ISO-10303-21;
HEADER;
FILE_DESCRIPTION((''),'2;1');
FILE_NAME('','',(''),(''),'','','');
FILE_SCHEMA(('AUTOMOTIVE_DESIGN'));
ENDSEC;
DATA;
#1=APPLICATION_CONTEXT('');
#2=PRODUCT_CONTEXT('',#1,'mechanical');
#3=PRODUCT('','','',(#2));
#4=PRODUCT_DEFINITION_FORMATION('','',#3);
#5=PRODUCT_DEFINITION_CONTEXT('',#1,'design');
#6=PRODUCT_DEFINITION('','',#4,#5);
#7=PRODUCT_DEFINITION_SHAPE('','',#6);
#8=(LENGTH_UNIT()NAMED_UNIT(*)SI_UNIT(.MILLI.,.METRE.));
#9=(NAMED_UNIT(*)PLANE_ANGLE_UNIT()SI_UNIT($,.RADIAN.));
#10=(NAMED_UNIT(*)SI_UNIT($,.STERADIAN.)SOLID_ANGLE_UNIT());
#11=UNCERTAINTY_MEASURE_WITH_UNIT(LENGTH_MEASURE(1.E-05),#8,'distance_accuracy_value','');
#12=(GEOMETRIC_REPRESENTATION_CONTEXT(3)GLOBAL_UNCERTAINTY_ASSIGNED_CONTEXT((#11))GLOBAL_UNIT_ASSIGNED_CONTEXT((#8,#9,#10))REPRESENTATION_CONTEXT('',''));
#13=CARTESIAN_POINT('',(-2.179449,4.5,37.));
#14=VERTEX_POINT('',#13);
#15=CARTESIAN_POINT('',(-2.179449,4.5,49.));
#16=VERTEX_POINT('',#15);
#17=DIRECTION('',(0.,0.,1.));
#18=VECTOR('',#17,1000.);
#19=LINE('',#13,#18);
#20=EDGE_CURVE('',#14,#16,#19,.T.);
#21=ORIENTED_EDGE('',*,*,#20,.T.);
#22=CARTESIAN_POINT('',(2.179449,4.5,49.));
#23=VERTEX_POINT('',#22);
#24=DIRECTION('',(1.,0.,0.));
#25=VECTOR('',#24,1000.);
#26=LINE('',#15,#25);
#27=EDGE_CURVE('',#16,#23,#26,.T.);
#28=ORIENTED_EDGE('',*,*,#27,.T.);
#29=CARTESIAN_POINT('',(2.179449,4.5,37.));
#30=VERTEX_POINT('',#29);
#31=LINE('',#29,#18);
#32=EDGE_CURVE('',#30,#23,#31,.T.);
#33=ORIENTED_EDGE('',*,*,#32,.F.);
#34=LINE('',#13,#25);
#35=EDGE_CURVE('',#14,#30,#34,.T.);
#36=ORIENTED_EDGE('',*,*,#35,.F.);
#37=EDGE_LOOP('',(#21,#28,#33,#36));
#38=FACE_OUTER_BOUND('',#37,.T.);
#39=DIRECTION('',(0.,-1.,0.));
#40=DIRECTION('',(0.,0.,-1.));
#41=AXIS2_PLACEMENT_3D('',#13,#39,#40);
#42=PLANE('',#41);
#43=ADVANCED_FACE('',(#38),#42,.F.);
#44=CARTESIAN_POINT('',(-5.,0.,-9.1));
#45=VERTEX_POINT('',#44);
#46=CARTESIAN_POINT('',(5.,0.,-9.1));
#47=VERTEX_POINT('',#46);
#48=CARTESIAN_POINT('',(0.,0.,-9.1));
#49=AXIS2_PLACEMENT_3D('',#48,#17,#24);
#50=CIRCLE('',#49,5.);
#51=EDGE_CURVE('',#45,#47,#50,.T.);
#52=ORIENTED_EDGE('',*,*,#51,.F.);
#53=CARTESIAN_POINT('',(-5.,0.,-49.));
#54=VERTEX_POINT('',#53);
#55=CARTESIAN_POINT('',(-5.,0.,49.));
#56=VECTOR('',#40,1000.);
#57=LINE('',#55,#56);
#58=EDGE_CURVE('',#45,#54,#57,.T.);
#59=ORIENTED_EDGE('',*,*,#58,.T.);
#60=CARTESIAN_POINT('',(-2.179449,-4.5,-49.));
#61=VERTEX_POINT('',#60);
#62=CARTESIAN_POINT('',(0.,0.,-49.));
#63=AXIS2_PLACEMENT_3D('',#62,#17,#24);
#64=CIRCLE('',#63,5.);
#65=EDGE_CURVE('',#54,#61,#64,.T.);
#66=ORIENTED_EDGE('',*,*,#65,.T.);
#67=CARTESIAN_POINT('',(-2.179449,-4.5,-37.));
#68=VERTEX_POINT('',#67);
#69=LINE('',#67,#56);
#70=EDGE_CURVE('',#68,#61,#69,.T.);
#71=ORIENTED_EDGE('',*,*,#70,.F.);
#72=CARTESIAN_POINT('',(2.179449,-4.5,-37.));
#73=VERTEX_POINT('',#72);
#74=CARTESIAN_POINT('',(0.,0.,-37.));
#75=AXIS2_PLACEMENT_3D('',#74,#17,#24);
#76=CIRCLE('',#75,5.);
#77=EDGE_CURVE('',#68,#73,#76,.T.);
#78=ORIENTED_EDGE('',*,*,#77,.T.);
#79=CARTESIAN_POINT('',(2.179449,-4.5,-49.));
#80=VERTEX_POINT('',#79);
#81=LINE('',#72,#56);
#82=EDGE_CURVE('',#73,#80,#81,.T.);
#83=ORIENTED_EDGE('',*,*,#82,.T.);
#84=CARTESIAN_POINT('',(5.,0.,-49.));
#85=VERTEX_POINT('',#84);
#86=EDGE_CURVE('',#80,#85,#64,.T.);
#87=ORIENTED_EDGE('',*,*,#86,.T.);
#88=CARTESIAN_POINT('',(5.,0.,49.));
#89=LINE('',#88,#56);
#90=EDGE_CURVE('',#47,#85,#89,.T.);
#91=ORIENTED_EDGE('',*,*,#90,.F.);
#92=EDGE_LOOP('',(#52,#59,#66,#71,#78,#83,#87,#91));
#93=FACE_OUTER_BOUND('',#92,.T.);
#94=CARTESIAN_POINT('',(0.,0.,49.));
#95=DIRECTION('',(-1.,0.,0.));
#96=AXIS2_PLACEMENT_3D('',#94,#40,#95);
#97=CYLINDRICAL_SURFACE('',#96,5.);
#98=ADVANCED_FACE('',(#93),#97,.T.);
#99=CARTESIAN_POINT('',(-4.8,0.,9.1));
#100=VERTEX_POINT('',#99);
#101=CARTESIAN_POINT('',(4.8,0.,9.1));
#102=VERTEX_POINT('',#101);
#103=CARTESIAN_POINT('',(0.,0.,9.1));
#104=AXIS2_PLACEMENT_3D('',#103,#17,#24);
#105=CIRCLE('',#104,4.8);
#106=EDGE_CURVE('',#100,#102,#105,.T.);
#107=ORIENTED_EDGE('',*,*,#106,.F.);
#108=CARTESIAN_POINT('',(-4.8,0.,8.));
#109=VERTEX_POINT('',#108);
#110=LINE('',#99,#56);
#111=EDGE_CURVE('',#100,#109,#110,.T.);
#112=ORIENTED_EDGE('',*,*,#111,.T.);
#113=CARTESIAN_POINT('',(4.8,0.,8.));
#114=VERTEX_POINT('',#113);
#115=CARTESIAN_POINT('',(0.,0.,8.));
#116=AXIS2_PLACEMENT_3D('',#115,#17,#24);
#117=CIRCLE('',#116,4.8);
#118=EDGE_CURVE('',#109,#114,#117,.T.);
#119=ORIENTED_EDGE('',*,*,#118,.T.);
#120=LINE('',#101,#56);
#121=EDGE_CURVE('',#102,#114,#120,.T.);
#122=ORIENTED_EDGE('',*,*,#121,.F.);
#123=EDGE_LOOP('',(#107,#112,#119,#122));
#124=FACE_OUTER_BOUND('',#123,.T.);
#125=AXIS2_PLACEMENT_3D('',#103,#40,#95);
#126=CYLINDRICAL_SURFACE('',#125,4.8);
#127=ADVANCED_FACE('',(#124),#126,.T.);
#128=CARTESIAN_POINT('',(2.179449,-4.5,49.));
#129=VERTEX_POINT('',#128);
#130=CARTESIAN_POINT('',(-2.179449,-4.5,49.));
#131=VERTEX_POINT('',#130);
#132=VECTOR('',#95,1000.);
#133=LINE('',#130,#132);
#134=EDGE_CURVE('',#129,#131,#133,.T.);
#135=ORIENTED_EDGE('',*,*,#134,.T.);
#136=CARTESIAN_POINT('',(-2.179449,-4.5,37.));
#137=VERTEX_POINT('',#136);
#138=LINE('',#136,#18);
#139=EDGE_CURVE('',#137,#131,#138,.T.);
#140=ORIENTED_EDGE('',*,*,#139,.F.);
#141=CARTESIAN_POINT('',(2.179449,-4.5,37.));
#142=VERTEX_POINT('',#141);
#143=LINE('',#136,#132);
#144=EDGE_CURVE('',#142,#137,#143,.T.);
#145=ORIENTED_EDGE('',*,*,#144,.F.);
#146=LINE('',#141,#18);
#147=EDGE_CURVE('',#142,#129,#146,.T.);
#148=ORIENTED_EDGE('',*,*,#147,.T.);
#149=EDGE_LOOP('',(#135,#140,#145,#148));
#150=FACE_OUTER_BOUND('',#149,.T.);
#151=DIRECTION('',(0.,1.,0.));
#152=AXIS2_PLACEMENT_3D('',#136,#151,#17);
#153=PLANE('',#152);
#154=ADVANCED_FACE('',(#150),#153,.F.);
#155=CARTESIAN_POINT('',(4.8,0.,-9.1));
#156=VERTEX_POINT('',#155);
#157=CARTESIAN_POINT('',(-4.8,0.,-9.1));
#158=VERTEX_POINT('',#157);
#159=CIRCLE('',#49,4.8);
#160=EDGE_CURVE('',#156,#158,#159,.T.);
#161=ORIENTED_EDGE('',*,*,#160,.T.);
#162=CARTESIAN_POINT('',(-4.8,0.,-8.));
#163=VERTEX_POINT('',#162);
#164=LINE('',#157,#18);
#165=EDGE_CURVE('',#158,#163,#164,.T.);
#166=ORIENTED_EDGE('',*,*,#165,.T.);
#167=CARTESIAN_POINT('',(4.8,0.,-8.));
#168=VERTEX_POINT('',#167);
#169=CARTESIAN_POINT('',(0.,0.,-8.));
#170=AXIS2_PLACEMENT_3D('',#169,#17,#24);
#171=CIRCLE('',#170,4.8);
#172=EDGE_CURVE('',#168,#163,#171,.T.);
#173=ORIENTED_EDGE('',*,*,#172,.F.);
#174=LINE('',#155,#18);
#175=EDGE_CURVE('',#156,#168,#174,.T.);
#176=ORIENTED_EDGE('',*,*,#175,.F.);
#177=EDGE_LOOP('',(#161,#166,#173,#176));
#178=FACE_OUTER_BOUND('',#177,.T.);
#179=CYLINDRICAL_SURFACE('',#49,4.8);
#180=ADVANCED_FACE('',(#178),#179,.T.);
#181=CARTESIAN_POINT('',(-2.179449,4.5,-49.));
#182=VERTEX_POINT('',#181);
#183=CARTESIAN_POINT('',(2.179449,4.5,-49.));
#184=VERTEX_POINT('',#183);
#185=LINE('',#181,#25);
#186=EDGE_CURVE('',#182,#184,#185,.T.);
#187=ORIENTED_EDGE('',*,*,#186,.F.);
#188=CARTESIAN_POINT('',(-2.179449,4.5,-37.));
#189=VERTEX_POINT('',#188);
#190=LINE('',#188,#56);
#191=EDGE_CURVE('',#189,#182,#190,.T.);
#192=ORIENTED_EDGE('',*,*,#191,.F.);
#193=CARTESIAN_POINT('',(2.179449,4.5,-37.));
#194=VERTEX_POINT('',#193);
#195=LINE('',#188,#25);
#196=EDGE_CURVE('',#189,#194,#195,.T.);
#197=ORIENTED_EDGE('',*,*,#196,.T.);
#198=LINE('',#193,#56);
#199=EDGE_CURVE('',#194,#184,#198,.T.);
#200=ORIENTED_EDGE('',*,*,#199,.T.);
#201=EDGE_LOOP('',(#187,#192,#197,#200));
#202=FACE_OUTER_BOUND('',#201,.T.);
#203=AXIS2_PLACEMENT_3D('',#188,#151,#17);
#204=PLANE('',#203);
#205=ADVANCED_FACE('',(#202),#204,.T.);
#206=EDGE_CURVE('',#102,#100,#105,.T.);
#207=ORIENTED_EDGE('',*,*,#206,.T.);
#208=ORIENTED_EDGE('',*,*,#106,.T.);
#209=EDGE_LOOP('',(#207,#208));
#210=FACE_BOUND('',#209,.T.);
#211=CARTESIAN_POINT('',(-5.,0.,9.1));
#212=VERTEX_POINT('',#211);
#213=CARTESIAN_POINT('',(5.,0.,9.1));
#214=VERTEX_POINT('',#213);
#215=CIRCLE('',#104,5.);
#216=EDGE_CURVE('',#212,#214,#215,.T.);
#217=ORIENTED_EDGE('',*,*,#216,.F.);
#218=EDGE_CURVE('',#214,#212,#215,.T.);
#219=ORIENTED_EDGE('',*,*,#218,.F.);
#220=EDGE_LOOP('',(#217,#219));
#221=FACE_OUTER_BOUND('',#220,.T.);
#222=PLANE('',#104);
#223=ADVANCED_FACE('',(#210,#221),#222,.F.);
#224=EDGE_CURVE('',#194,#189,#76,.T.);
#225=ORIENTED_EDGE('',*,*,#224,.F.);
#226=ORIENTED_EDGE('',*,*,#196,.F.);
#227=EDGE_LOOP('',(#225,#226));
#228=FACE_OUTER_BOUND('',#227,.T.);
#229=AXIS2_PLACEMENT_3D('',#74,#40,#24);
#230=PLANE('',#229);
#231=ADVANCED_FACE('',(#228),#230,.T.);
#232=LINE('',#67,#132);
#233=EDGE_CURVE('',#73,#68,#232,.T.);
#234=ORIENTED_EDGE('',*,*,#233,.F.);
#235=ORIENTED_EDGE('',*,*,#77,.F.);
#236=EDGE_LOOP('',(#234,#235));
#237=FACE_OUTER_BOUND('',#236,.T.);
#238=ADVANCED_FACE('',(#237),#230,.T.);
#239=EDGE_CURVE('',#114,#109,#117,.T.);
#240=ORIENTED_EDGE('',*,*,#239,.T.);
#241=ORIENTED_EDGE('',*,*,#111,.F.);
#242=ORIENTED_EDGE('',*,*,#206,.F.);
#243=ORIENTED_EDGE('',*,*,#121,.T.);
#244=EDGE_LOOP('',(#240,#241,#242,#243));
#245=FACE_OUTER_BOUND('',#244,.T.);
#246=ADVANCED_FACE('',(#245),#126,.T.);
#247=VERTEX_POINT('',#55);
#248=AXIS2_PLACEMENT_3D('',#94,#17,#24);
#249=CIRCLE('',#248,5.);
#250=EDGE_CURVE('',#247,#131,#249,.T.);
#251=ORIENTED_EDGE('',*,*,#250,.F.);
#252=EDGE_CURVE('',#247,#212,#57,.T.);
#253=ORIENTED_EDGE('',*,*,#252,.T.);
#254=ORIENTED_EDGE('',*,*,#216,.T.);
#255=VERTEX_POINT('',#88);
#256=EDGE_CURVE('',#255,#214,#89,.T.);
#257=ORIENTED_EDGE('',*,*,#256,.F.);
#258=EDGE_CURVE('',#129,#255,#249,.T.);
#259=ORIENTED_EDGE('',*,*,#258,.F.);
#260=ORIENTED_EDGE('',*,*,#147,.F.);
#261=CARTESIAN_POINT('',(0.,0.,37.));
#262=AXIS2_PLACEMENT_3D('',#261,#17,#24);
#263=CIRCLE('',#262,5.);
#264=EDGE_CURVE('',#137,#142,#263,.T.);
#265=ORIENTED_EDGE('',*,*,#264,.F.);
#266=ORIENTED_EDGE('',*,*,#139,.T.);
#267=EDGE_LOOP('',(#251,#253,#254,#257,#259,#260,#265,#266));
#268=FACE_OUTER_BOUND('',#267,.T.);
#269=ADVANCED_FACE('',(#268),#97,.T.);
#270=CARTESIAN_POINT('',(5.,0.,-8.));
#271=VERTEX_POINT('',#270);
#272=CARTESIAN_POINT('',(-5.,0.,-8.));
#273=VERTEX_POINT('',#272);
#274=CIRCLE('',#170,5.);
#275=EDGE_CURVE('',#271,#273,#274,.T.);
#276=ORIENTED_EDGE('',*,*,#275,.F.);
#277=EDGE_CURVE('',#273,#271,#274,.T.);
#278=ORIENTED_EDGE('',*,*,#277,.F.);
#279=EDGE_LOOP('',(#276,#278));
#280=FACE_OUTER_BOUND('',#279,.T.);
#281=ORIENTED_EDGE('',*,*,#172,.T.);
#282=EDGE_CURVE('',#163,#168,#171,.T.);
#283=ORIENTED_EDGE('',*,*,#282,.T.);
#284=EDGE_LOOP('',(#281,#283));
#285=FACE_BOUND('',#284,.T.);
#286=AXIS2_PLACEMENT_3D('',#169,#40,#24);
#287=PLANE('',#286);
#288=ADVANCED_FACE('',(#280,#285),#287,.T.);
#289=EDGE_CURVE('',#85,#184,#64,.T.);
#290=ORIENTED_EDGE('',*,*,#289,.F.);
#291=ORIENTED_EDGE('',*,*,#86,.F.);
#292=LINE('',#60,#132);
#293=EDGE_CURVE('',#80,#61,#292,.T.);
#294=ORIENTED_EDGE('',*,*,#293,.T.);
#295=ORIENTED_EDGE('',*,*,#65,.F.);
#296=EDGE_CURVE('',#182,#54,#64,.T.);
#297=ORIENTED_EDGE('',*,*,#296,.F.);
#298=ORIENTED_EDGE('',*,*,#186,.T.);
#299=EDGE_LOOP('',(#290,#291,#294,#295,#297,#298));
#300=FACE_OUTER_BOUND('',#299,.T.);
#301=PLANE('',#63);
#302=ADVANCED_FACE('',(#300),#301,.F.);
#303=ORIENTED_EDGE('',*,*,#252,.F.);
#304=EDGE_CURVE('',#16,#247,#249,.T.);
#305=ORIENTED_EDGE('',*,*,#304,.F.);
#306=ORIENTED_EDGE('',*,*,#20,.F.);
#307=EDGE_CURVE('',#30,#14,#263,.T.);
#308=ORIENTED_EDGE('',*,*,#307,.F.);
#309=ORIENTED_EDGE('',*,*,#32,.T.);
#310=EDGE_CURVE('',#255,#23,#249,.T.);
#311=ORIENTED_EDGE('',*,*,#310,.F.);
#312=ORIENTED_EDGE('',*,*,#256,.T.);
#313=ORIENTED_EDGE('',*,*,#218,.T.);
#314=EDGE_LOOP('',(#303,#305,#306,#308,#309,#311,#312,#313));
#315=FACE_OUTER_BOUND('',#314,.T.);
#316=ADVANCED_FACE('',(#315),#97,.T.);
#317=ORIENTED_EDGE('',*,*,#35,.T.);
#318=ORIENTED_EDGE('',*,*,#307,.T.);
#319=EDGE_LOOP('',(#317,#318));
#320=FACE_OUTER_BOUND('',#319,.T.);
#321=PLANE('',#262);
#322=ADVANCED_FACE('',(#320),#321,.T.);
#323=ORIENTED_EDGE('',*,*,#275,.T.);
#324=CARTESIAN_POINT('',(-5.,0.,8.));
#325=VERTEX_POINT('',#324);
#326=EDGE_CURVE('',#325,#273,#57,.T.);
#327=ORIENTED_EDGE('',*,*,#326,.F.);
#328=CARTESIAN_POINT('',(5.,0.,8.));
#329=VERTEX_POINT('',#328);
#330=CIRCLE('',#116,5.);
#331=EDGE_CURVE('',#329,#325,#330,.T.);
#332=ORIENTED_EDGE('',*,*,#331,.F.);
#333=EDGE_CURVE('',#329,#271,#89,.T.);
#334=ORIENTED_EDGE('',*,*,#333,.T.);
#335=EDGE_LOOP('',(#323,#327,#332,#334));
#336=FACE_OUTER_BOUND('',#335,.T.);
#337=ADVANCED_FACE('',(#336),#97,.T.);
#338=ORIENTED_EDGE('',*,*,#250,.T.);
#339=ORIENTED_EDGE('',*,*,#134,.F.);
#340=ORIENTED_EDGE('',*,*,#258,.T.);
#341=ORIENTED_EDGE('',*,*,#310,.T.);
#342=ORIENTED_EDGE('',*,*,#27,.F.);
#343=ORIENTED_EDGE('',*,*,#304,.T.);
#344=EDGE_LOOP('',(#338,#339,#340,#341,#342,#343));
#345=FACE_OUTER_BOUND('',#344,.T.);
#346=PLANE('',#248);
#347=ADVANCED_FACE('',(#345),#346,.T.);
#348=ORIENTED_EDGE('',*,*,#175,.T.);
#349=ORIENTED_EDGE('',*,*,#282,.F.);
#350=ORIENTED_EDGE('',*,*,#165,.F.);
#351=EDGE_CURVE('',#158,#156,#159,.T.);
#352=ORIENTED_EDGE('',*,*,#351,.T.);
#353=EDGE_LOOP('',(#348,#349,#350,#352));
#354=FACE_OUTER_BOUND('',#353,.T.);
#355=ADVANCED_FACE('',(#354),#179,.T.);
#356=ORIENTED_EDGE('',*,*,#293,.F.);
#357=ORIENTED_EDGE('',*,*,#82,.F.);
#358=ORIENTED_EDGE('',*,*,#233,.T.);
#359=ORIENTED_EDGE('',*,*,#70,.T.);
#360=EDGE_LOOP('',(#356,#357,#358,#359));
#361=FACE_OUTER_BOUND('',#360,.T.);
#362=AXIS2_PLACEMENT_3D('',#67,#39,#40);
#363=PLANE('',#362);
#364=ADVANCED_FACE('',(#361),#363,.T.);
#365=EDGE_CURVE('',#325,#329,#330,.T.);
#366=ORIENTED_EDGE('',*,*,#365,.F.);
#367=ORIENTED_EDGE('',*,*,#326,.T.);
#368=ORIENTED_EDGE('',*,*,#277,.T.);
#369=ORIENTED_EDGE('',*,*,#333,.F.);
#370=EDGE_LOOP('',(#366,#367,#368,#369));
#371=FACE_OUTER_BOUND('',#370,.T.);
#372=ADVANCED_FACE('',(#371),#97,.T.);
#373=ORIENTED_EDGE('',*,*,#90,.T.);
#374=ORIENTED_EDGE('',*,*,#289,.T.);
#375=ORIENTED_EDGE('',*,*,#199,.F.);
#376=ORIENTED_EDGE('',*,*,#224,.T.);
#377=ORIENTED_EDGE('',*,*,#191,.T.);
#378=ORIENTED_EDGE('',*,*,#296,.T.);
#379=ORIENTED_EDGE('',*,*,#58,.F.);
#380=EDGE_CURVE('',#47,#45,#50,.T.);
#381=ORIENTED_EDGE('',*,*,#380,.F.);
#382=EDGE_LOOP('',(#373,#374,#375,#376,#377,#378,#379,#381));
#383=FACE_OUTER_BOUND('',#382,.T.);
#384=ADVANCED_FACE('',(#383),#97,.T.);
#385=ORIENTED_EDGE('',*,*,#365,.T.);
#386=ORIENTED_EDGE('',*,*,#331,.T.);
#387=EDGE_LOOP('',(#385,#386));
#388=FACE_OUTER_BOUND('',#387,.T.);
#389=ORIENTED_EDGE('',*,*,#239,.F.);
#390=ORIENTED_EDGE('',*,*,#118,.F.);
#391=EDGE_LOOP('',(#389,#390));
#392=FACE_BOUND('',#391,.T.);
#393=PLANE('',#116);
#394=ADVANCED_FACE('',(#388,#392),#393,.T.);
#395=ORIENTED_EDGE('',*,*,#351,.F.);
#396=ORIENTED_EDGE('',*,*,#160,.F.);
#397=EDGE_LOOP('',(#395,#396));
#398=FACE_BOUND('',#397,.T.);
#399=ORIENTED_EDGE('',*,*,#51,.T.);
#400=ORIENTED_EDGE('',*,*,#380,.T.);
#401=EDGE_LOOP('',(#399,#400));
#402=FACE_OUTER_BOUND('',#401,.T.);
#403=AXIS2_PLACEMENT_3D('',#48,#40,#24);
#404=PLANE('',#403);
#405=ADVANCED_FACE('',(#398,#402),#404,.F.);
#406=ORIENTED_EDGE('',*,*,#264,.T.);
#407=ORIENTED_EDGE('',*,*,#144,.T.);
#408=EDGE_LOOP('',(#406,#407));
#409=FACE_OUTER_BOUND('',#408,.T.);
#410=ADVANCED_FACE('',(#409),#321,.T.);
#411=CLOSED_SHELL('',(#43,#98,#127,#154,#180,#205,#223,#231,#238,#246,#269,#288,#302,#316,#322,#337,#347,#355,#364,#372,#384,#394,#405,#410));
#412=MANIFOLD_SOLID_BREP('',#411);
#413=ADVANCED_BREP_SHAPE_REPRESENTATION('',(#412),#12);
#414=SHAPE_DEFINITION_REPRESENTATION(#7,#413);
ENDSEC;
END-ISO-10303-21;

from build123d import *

# Parameters (mm, degrees)
SKETCH_1_R          = 5
EXTRUDE_1_DEPTH     = 49
CUT_EXTRUDE_START   = 1.1
SKETCH_3_R          = 5
SKETCH_3_R_2        = 4.8
CUT_EXTRUDE_2_DEPTH = 1.1
CUT_EXTRUDE_1_DEPTH = 12


with BuildPart() as part:
    # 草图1 → 凸台-拉伸1 (new, symmetric)
    with BuildSketch(Plane.XY):
        Circle(SKETCH_1_R)
    extrude(amount=EXTRUDE_1_DEPTH, both=True)

    # 草图3 → 切除-拉伸2 (cut)
    with BuildSketch(Plane.XY.offset(8).offset(CUT_EXTRUDE_START)):
        Circle(SKETCH_3_R)
        Circle(SKETCH_3_R_2, mode=Mode.SUBTRACT)
    cut_extrude_2 = extrude(amount=-CUT_EXTRUDE_2_DEPTH, mode=Mode.SUBTRACT)

    # 镜向2: 切除-拉伸2 across plane
    add(cut_extrude_2.mirror(Plane.XY), mode=Mode.SUBTRACT)

    # 草图2 → 切除-拉伸1 (cut)
    with BuildSketch(Plane.XY.offset(49)):
        with BuildLine():
            Line((-2.179449472, 4.5), (2.179449472, 4.5))
            ThreePointArc((2.179449472, 4.5), (0, 5), (-2.179449472, 4.5))
        make_face()
        with BuildLine():
            Line((-2.179449472, -4.5), (2.179449472, -4.5))
            ThreePointArc((2.179449472, -4.5), (0, -5), (-2.179449472, -4.5))
        make_face()
    cut_extrude_1 = extrude(amount=-CUT_EXTRUDE_1_DEPTH, mode=Mode.SUBTRACT)

    # 镜向1: 切除-拉伸1 across plane
    add(cut_extrude_1.mirror(Plane.XY), mode=Mode.SUBTRACT)


solid = part.part
